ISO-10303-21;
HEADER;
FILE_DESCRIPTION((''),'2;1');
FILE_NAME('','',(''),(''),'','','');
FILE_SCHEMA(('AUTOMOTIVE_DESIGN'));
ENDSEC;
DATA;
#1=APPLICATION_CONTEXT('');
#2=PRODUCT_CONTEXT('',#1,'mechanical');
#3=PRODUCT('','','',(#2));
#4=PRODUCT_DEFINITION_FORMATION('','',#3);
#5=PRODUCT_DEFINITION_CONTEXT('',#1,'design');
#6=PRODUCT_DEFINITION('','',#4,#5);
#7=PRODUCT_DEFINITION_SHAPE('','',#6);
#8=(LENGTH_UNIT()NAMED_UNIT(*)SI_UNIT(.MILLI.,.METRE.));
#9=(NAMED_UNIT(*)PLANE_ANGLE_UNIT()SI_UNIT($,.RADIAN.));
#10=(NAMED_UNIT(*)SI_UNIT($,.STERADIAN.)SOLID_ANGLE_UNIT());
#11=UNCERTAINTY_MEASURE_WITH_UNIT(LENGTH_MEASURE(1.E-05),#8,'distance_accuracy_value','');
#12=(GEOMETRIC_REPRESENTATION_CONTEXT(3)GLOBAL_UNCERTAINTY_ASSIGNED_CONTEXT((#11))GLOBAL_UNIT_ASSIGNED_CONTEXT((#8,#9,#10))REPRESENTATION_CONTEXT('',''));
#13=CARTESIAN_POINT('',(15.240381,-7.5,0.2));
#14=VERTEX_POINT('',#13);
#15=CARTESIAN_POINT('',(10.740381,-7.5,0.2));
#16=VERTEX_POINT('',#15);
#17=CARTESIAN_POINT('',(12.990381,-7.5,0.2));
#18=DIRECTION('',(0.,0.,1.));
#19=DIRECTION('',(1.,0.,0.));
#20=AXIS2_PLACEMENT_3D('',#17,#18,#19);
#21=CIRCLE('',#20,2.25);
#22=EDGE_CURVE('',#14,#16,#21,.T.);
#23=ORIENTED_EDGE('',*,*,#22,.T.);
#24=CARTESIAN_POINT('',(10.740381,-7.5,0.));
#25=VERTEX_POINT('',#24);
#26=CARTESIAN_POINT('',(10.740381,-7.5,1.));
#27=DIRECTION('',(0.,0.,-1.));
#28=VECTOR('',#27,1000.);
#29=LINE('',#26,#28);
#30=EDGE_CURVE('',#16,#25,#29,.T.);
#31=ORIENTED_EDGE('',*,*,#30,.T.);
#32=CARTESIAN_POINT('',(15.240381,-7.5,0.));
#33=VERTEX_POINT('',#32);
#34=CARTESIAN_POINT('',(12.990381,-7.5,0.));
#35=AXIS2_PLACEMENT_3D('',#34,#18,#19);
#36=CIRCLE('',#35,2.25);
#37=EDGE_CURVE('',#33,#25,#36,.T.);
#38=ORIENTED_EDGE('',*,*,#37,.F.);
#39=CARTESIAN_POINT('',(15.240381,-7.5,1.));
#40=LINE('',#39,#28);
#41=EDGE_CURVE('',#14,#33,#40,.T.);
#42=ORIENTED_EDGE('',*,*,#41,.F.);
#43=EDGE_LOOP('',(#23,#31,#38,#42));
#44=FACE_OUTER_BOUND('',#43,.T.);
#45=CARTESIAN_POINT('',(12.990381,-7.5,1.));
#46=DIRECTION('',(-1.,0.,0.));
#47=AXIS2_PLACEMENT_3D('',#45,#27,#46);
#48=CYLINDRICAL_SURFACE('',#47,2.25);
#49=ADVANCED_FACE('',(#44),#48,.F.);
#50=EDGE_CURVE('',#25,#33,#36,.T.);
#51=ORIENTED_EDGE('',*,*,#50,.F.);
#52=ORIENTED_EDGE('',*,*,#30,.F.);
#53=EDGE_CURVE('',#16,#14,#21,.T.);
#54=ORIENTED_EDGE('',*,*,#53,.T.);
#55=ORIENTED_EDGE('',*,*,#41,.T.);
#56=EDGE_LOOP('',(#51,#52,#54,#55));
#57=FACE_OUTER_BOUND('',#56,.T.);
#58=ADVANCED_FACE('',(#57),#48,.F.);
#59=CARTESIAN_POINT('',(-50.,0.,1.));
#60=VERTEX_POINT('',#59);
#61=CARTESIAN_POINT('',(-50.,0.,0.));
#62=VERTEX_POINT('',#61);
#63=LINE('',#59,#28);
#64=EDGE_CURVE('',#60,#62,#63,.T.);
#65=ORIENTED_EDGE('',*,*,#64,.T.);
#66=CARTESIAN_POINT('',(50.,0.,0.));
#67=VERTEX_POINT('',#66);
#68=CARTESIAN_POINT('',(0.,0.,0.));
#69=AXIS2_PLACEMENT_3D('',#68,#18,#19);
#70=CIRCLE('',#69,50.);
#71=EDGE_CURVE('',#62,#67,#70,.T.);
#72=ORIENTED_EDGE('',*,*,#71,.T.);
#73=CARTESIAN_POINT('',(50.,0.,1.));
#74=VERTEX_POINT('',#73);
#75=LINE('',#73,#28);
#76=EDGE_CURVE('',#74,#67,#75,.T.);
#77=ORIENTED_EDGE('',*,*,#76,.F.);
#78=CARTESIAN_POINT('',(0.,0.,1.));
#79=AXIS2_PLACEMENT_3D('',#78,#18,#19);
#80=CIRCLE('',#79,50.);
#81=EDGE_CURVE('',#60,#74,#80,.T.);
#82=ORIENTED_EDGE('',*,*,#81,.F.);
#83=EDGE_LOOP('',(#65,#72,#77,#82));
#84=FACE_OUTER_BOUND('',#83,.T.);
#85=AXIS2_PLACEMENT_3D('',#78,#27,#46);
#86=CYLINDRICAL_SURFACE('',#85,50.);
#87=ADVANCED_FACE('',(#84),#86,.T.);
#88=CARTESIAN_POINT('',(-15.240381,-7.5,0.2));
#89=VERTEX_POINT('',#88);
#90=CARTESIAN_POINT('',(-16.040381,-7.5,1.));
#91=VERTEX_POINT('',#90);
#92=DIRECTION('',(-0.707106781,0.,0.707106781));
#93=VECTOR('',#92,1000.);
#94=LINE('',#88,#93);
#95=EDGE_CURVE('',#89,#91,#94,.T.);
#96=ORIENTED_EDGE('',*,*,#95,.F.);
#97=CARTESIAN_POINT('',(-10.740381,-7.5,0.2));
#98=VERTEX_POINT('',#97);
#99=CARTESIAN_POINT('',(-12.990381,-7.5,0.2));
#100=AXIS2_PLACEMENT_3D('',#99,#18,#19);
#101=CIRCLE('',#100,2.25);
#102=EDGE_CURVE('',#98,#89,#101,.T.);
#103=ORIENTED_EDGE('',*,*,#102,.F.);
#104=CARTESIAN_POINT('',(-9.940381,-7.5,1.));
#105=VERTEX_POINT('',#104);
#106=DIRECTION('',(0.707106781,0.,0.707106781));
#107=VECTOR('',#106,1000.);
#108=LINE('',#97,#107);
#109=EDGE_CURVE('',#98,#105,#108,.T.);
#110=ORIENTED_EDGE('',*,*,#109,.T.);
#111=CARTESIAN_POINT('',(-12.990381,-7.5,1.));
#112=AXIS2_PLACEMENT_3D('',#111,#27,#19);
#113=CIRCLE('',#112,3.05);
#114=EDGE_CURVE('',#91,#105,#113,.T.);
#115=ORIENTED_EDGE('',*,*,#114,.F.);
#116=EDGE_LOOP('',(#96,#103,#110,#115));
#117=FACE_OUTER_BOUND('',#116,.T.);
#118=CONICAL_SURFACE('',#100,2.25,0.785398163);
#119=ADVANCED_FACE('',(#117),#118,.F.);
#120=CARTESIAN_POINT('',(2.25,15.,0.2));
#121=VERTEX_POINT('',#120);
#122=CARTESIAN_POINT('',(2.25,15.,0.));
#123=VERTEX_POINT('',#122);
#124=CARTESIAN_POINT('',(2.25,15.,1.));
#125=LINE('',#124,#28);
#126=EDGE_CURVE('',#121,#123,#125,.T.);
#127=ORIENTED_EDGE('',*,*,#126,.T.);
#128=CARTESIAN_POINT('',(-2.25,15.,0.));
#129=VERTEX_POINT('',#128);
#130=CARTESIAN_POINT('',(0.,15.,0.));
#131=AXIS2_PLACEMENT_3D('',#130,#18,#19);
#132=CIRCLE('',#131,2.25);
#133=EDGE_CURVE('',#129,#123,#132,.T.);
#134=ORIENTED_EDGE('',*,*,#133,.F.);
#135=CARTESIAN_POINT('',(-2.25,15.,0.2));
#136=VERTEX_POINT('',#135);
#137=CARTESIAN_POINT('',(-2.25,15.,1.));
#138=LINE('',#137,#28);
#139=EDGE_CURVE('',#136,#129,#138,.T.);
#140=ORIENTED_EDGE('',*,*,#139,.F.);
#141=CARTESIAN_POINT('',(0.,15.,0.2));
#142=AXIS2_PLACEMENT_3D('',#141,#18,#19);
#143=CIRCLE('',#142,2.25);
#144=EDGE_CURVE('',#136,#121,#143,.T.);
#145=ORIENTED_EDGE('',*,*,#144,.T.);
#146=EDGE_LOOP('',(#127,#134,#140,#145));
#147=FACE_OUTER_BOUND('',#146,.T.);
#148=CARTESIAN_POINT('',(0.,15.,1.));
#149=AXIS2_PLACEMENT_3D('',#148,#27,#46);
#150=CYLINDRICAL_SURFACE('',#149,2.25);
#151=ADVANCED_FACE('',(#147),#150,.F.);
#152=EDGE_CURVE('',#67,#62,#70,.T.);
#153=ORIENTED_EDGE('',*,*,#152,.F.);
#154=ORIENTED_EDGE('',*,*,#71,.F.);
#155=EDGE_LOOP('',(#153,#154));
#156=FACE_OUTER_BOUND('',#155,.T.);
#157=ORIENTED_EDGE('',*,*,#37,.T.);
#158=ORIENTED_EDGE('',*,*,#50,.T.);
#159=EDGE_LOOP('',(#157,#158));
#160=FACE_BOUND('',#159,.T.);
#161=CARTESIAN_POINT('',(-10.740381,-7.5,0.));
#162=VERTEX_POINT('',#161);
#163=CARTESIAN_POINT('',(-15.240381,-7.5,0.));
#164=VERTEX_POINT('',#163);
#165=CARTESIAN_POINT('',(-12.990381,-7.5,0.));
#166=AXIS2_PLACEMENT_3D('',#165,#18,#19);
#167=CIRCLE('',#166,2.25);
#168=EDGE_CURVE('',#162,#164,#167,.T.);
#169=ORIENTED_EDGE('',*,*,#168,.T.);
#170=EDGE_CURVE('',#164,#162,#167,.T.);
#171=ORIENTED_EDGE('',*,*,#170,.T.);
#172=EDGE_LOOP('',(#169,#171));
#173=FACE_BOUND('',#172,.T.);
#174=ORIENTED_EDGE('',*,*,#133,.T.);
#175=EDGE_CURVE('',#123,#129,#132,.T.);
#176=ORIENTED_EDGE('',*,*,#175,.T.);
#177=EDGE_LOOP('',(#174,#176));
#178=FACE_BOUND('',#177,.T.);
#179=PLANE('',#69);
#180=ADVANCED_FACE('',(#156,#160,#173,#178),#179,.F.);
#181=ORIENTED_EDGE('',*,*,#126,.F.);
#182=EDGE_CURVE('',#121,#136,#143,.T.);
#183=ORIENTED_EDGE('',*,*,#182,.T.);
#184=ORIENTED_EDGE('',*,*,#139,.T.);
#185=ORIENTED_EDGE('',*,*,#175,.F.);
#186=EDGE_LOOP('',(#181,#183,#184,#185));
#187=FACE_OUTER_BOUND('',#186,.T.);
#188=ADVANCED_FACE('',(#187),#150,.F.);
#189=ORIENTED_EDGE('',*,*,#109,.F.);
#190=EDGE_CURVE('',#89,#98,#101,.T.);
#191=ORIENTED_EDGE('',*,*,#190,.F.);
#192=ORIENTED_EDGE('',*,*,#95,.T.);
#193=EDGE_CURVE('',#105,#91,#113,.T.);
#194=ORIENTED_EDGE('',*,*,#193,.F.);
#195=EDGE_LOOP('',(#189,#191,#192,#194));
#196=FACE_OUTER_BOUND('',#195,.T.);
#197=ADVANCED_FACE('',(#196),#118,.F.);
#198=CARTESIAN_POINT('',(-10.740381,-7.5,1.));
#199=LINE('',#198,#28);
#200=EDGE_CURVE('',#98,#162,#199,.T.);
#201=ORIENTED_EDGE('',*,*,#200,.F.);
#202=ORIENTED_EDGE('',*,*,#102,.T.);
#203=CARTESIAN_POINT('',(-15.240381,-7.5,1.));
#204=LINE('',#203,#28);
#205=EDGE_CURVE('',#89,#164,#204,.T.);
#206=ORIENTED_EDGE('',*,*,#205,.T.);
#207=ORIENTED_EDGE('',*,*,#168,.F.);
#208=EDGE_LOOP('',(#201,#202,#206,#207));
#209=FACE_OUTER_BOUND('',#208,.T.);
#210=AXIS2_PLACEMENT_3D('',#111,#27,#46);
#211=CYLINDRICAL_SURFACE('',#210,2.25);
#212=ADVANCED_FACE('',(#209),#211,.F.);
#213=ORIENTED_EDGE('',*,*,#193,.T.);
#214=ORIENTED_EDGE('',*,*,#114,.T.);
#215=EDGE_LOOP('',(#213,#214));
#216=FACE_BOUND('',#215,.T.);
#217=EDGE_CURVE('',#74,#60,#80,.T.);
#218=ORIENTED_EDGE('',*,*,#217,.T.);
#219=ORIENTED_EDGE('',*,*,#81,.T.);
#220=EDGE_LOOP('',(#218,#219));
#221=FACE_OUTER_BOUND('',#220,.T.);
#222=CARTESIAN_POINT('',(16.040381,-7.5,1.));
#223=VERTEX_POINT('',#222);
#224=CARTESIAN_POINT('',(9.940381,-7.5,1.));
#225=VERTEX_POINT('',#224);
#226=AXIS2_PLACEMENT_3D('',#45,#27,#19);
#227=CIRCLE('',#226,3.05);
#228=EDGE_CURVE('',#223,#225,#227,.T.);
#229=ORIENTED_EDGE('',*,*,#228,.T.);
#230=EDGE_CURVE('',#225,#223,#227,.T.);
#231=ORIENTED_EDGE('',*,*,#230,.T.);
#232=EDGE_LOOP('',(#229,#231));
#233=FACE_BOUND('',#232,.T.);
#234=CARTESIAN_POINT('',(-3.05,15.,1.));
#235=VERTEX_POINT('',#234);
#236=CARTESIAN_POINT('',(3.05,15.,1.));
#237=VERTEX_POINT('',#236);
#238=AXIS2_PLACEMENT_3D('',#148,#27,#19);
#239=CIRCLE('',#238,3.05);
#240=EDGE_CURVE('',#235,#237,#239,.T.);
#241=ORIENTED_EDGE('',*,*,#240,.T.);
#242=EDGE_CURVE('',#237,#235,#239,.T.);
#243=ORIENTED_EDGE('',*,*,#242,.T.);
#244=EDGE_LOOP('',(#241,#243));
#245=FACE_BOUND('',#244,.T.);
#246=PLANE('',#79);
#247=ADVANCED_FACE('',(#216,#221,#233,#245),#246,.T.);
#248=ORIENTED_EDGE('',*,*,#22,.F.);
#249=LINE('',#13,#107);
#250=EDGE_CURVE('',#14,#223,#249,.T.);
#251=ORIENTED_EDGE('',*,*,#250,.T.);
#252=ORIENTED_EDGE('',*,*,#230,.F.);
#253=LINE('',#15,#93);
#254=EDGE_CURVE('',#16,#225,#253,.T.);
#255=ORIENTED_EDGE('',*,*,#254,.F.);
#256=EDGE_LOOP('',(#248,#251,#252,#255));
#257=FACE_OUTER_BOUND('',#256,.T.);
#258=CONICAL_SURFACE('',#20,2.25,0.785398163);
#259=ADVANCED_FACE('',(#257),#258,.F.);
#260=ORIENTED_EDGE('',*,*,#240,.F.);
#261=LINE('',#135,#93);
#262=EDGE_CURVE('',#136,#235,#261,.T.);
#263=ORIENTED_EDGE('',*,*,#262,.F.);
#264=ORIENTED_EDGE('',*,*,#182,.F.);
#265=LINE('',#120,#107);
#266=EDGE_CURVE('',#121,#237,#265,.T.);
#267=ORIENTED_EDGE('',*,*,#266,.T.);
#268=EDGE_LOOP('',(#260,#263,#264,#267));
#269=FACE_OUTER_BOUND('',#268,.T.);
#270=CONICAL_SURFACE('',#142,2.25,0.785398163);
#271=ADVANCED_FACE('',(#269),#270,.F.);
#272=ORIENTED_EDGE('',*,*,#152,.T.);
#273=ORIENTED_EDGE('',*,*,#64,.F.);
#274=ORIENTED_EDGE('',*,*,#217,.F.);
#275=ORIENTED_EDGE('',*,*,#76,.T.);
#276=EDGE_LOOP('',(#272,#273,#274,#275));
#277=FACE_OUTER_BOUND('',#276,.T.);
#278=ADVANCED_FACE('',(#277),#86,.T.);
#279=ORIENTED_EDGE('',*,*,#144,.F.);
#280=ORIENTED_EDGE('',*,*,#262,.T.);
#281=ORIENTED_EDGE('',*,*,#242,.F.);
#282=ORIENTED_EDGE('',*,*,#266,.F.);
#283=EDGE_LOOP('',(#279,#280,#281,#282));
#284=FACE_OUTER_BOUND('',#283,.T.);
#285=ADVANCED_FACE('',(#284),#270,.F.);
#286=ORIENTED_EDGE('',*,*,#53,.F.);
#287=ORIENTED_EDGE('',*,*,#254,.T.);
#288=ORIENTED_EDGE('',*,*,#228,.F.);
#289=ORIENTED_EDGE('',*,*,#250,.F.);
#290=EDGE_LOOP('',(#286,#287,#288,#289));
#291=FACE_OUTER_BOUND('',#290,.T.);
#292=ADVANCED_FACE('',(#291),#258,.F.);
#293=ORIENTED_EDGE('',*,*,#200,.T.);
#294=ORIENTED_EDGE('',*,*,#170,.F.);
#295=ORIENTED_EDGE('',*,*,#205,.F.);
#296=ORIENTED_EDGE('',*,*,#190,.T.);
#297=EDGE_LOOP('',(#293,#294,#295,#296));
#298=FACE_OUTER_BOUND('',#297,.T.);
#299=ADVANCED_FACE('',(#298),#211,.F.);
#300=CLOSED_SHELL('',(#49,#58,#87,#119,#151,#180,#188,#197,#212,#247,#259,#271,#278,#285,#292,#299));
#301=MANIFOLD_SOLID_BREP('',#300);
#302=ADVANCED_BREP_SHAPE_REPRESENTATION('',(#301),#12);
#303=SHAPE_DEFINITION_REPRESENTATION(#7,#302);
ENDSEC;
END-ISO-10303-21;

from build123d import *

# Parameters (mm, degrees)
SKETCH_1_R      = 50
SKETCH_1_R_2    = 2.25
EXTRUDE_1_DEPTH = 1
CHAMFER_1_SIZE  = 0.8


with BuildPart() as part:
    # 草图1 → 凸台-拉伸1 (new body)
    with BuildSketch(Plane.XY):
        Circle(SKETCH_1_R)
        with Locations((0, 15)):
            Circle(SKETCH_1_R_2, mode=Mode.SUBTRACT)
        with Locations((12.990381057, -7.5)):
            Circle(SKETCH_1_R_2, mode=Mode.SUBTRACT)
        with Locations((-12.990381057, -7.5)):
            Circle(SKETCH_1_R_2, mode=Mode.SUBTRACT)
    extrude(amount=EXTRUDE_1_DEPTH)

    # 倒角1
    chamfer_1_edges = [part.edges().sort_by_distance(p)[0] for p in [
        (-15.240381057, -7.5, 1),
        (-2.25, 15, 1),
        (10.740381057, -7.5, 1),
    ]]
    chamfer(chamfer_1_edges, length=CHAMFER_1_SIZE)


solid = part.part
